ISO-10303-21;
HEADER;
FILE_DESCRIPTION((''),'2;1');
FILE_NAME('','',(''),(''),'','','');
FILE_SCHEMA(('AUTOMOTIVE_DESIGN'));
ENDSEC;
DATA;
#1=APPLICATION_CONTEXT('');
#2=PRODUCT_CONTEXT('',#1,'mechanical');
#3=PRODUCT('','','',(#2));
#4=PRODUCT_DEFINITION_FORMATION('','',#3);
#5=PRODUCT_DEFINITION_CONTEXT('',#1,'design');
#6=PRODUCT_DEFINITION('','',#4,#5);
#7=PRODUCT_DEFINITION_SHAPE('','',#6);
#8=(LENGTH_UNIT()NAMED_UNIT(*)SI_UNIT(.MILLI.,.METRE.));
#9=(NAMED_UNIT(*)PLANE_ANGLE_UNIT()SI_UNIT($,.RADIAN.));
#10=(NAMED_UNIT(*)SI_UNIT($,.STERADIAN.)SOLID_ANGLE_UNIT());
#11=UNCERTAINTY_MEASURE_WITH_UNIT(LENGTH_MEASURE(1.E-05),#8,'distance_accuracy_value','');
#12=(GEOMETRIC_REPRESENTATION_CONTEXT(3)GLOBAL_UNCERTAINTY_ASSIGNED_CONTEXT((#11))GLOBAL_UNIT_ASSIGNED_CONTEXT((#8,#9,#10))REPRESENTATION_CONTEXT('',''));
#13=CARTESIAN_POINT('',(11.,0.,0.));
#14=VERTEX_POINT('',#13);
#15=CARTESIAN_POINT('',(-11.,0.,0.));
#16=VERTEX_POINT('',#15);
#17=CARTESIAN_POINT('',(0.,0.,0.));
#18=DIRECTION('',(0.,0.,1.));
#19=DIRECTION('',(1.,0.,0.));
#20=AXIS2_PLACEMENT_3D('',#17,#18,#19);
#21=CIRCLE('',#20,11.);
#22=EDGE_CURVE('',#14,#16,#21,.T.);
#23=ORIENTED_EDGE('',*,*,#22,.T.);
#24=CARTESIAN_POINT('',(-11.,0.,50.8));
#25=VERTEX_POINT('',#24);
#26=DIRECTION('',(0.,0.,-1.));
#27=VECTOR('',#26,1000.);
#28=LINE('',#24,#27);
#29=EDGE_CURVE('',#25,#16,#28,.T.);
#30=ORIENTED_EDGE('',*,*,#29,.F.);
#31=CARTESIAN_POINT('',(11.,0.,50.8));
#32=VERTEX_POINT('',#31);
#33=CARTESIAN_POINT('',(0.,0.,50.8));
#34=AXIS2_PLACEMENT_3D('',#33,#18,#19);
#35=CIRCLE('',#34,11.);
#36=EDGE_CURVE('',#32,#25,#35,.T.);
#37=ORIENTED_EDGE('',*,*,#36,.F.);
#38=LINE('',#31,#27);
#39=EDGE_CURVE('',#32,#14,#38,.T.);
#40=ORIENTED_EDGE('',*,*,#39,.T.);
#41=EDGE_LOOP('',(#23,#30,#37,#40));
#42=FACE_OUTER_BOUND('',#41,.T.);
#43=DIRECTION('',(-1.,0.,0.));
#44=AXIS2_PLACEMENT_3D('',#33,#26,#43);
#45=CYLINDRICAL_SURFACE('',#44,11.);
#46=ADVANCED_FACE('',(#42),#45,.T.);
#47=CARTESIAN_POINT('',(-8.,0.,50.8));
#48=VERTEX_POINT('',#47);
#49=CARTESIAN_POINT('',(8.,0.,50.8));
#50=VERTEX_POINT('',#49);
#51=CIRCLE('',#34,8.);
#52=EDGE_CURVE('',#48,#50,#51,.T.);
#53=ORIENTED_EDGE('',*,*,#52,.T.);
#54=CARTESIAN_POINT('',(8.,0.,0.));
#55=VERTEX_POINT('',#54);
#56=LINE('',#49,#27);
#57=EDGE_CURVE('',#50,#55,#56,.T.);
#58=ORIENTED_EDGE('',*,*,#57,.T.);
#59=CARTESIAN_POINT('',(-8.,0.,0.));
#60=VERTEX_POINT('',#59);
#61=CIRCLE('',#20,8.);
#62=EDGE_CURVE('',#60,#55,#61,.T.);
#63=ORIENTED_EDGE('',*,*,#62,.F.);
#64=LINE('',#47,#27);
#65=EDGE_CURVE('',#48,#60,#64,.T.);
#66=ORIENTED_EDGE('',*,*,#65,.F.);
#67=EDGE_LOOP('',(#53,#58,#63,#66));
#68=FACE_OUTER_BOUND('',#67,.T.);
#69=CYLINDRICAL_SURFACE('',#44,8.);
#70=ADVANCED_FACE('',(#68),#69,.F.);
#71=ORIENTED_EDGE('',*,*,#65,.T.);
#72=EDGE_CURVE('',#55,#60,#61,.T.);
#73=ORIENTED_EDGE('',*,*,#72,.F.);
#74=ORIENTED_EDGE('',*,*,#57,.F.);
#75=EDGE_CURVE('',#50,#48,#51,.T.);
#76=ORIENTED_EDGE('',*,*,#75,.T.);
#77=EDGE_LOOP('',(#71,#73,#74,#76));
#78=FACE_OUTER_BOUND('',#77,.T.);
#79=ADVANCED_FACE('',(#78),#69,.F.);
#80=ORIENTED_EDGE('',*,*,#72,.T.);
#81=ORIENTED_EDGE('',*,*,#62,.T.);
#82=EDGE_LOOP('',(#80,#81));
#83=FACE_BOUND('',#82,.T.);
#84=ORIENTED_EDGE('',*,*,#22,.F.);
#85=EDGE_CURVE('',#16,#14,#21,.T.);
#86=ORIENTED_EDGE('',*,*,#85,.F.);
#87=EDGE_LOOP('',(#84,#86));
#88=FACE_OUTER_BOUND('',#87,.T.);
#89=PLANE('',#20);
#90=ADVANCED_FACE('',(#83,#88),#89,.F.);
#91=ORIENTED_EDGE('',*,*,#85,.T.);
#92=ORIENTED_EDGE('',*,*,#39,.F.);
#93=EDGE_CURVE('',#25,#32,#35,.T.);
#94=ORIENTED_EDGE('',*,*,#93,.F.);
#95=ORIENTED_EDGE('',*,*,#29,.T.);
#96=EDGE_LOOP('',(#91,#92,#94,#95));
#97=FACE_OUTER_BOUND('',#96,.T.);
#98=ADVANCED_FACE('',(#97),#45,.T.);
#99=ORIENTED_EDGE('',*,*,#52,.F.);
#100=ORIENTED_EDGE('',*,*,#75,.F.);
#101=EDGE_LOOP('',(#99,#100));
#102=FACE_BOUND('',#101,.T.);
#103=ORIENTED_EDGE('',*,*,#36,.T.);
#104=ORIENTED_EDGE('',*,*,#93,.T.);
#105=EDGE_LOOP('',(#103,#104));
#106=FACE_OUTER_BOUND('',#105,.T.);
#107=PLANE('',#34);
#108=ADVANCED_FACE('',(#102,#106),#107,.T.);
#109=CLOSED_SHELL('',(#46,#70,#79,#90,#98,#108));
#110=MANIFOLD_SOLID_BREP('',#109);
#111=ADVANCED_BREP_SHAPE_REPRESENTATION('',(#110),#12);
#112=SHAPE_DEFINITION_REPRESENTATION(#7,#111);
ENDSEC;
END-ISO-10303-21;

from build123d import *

# Parameters (mm, degrees)
SKETCH1_R      = 11
SKETCH1_R_2    = 8
EXTRUDE1_DEPTH = 50.8


with BuildPart() as part:
    # Sketch1 → Extrude1 (new body)
    with BuildSketch(Plane.XY):
        Circle(SKETCH1_R)
        Circle(SKETCH1_R_2, mode=Mode.SUBTRACT)
    extrude(amount=EXTRUDE1_DEPTH)


solid = part.part
